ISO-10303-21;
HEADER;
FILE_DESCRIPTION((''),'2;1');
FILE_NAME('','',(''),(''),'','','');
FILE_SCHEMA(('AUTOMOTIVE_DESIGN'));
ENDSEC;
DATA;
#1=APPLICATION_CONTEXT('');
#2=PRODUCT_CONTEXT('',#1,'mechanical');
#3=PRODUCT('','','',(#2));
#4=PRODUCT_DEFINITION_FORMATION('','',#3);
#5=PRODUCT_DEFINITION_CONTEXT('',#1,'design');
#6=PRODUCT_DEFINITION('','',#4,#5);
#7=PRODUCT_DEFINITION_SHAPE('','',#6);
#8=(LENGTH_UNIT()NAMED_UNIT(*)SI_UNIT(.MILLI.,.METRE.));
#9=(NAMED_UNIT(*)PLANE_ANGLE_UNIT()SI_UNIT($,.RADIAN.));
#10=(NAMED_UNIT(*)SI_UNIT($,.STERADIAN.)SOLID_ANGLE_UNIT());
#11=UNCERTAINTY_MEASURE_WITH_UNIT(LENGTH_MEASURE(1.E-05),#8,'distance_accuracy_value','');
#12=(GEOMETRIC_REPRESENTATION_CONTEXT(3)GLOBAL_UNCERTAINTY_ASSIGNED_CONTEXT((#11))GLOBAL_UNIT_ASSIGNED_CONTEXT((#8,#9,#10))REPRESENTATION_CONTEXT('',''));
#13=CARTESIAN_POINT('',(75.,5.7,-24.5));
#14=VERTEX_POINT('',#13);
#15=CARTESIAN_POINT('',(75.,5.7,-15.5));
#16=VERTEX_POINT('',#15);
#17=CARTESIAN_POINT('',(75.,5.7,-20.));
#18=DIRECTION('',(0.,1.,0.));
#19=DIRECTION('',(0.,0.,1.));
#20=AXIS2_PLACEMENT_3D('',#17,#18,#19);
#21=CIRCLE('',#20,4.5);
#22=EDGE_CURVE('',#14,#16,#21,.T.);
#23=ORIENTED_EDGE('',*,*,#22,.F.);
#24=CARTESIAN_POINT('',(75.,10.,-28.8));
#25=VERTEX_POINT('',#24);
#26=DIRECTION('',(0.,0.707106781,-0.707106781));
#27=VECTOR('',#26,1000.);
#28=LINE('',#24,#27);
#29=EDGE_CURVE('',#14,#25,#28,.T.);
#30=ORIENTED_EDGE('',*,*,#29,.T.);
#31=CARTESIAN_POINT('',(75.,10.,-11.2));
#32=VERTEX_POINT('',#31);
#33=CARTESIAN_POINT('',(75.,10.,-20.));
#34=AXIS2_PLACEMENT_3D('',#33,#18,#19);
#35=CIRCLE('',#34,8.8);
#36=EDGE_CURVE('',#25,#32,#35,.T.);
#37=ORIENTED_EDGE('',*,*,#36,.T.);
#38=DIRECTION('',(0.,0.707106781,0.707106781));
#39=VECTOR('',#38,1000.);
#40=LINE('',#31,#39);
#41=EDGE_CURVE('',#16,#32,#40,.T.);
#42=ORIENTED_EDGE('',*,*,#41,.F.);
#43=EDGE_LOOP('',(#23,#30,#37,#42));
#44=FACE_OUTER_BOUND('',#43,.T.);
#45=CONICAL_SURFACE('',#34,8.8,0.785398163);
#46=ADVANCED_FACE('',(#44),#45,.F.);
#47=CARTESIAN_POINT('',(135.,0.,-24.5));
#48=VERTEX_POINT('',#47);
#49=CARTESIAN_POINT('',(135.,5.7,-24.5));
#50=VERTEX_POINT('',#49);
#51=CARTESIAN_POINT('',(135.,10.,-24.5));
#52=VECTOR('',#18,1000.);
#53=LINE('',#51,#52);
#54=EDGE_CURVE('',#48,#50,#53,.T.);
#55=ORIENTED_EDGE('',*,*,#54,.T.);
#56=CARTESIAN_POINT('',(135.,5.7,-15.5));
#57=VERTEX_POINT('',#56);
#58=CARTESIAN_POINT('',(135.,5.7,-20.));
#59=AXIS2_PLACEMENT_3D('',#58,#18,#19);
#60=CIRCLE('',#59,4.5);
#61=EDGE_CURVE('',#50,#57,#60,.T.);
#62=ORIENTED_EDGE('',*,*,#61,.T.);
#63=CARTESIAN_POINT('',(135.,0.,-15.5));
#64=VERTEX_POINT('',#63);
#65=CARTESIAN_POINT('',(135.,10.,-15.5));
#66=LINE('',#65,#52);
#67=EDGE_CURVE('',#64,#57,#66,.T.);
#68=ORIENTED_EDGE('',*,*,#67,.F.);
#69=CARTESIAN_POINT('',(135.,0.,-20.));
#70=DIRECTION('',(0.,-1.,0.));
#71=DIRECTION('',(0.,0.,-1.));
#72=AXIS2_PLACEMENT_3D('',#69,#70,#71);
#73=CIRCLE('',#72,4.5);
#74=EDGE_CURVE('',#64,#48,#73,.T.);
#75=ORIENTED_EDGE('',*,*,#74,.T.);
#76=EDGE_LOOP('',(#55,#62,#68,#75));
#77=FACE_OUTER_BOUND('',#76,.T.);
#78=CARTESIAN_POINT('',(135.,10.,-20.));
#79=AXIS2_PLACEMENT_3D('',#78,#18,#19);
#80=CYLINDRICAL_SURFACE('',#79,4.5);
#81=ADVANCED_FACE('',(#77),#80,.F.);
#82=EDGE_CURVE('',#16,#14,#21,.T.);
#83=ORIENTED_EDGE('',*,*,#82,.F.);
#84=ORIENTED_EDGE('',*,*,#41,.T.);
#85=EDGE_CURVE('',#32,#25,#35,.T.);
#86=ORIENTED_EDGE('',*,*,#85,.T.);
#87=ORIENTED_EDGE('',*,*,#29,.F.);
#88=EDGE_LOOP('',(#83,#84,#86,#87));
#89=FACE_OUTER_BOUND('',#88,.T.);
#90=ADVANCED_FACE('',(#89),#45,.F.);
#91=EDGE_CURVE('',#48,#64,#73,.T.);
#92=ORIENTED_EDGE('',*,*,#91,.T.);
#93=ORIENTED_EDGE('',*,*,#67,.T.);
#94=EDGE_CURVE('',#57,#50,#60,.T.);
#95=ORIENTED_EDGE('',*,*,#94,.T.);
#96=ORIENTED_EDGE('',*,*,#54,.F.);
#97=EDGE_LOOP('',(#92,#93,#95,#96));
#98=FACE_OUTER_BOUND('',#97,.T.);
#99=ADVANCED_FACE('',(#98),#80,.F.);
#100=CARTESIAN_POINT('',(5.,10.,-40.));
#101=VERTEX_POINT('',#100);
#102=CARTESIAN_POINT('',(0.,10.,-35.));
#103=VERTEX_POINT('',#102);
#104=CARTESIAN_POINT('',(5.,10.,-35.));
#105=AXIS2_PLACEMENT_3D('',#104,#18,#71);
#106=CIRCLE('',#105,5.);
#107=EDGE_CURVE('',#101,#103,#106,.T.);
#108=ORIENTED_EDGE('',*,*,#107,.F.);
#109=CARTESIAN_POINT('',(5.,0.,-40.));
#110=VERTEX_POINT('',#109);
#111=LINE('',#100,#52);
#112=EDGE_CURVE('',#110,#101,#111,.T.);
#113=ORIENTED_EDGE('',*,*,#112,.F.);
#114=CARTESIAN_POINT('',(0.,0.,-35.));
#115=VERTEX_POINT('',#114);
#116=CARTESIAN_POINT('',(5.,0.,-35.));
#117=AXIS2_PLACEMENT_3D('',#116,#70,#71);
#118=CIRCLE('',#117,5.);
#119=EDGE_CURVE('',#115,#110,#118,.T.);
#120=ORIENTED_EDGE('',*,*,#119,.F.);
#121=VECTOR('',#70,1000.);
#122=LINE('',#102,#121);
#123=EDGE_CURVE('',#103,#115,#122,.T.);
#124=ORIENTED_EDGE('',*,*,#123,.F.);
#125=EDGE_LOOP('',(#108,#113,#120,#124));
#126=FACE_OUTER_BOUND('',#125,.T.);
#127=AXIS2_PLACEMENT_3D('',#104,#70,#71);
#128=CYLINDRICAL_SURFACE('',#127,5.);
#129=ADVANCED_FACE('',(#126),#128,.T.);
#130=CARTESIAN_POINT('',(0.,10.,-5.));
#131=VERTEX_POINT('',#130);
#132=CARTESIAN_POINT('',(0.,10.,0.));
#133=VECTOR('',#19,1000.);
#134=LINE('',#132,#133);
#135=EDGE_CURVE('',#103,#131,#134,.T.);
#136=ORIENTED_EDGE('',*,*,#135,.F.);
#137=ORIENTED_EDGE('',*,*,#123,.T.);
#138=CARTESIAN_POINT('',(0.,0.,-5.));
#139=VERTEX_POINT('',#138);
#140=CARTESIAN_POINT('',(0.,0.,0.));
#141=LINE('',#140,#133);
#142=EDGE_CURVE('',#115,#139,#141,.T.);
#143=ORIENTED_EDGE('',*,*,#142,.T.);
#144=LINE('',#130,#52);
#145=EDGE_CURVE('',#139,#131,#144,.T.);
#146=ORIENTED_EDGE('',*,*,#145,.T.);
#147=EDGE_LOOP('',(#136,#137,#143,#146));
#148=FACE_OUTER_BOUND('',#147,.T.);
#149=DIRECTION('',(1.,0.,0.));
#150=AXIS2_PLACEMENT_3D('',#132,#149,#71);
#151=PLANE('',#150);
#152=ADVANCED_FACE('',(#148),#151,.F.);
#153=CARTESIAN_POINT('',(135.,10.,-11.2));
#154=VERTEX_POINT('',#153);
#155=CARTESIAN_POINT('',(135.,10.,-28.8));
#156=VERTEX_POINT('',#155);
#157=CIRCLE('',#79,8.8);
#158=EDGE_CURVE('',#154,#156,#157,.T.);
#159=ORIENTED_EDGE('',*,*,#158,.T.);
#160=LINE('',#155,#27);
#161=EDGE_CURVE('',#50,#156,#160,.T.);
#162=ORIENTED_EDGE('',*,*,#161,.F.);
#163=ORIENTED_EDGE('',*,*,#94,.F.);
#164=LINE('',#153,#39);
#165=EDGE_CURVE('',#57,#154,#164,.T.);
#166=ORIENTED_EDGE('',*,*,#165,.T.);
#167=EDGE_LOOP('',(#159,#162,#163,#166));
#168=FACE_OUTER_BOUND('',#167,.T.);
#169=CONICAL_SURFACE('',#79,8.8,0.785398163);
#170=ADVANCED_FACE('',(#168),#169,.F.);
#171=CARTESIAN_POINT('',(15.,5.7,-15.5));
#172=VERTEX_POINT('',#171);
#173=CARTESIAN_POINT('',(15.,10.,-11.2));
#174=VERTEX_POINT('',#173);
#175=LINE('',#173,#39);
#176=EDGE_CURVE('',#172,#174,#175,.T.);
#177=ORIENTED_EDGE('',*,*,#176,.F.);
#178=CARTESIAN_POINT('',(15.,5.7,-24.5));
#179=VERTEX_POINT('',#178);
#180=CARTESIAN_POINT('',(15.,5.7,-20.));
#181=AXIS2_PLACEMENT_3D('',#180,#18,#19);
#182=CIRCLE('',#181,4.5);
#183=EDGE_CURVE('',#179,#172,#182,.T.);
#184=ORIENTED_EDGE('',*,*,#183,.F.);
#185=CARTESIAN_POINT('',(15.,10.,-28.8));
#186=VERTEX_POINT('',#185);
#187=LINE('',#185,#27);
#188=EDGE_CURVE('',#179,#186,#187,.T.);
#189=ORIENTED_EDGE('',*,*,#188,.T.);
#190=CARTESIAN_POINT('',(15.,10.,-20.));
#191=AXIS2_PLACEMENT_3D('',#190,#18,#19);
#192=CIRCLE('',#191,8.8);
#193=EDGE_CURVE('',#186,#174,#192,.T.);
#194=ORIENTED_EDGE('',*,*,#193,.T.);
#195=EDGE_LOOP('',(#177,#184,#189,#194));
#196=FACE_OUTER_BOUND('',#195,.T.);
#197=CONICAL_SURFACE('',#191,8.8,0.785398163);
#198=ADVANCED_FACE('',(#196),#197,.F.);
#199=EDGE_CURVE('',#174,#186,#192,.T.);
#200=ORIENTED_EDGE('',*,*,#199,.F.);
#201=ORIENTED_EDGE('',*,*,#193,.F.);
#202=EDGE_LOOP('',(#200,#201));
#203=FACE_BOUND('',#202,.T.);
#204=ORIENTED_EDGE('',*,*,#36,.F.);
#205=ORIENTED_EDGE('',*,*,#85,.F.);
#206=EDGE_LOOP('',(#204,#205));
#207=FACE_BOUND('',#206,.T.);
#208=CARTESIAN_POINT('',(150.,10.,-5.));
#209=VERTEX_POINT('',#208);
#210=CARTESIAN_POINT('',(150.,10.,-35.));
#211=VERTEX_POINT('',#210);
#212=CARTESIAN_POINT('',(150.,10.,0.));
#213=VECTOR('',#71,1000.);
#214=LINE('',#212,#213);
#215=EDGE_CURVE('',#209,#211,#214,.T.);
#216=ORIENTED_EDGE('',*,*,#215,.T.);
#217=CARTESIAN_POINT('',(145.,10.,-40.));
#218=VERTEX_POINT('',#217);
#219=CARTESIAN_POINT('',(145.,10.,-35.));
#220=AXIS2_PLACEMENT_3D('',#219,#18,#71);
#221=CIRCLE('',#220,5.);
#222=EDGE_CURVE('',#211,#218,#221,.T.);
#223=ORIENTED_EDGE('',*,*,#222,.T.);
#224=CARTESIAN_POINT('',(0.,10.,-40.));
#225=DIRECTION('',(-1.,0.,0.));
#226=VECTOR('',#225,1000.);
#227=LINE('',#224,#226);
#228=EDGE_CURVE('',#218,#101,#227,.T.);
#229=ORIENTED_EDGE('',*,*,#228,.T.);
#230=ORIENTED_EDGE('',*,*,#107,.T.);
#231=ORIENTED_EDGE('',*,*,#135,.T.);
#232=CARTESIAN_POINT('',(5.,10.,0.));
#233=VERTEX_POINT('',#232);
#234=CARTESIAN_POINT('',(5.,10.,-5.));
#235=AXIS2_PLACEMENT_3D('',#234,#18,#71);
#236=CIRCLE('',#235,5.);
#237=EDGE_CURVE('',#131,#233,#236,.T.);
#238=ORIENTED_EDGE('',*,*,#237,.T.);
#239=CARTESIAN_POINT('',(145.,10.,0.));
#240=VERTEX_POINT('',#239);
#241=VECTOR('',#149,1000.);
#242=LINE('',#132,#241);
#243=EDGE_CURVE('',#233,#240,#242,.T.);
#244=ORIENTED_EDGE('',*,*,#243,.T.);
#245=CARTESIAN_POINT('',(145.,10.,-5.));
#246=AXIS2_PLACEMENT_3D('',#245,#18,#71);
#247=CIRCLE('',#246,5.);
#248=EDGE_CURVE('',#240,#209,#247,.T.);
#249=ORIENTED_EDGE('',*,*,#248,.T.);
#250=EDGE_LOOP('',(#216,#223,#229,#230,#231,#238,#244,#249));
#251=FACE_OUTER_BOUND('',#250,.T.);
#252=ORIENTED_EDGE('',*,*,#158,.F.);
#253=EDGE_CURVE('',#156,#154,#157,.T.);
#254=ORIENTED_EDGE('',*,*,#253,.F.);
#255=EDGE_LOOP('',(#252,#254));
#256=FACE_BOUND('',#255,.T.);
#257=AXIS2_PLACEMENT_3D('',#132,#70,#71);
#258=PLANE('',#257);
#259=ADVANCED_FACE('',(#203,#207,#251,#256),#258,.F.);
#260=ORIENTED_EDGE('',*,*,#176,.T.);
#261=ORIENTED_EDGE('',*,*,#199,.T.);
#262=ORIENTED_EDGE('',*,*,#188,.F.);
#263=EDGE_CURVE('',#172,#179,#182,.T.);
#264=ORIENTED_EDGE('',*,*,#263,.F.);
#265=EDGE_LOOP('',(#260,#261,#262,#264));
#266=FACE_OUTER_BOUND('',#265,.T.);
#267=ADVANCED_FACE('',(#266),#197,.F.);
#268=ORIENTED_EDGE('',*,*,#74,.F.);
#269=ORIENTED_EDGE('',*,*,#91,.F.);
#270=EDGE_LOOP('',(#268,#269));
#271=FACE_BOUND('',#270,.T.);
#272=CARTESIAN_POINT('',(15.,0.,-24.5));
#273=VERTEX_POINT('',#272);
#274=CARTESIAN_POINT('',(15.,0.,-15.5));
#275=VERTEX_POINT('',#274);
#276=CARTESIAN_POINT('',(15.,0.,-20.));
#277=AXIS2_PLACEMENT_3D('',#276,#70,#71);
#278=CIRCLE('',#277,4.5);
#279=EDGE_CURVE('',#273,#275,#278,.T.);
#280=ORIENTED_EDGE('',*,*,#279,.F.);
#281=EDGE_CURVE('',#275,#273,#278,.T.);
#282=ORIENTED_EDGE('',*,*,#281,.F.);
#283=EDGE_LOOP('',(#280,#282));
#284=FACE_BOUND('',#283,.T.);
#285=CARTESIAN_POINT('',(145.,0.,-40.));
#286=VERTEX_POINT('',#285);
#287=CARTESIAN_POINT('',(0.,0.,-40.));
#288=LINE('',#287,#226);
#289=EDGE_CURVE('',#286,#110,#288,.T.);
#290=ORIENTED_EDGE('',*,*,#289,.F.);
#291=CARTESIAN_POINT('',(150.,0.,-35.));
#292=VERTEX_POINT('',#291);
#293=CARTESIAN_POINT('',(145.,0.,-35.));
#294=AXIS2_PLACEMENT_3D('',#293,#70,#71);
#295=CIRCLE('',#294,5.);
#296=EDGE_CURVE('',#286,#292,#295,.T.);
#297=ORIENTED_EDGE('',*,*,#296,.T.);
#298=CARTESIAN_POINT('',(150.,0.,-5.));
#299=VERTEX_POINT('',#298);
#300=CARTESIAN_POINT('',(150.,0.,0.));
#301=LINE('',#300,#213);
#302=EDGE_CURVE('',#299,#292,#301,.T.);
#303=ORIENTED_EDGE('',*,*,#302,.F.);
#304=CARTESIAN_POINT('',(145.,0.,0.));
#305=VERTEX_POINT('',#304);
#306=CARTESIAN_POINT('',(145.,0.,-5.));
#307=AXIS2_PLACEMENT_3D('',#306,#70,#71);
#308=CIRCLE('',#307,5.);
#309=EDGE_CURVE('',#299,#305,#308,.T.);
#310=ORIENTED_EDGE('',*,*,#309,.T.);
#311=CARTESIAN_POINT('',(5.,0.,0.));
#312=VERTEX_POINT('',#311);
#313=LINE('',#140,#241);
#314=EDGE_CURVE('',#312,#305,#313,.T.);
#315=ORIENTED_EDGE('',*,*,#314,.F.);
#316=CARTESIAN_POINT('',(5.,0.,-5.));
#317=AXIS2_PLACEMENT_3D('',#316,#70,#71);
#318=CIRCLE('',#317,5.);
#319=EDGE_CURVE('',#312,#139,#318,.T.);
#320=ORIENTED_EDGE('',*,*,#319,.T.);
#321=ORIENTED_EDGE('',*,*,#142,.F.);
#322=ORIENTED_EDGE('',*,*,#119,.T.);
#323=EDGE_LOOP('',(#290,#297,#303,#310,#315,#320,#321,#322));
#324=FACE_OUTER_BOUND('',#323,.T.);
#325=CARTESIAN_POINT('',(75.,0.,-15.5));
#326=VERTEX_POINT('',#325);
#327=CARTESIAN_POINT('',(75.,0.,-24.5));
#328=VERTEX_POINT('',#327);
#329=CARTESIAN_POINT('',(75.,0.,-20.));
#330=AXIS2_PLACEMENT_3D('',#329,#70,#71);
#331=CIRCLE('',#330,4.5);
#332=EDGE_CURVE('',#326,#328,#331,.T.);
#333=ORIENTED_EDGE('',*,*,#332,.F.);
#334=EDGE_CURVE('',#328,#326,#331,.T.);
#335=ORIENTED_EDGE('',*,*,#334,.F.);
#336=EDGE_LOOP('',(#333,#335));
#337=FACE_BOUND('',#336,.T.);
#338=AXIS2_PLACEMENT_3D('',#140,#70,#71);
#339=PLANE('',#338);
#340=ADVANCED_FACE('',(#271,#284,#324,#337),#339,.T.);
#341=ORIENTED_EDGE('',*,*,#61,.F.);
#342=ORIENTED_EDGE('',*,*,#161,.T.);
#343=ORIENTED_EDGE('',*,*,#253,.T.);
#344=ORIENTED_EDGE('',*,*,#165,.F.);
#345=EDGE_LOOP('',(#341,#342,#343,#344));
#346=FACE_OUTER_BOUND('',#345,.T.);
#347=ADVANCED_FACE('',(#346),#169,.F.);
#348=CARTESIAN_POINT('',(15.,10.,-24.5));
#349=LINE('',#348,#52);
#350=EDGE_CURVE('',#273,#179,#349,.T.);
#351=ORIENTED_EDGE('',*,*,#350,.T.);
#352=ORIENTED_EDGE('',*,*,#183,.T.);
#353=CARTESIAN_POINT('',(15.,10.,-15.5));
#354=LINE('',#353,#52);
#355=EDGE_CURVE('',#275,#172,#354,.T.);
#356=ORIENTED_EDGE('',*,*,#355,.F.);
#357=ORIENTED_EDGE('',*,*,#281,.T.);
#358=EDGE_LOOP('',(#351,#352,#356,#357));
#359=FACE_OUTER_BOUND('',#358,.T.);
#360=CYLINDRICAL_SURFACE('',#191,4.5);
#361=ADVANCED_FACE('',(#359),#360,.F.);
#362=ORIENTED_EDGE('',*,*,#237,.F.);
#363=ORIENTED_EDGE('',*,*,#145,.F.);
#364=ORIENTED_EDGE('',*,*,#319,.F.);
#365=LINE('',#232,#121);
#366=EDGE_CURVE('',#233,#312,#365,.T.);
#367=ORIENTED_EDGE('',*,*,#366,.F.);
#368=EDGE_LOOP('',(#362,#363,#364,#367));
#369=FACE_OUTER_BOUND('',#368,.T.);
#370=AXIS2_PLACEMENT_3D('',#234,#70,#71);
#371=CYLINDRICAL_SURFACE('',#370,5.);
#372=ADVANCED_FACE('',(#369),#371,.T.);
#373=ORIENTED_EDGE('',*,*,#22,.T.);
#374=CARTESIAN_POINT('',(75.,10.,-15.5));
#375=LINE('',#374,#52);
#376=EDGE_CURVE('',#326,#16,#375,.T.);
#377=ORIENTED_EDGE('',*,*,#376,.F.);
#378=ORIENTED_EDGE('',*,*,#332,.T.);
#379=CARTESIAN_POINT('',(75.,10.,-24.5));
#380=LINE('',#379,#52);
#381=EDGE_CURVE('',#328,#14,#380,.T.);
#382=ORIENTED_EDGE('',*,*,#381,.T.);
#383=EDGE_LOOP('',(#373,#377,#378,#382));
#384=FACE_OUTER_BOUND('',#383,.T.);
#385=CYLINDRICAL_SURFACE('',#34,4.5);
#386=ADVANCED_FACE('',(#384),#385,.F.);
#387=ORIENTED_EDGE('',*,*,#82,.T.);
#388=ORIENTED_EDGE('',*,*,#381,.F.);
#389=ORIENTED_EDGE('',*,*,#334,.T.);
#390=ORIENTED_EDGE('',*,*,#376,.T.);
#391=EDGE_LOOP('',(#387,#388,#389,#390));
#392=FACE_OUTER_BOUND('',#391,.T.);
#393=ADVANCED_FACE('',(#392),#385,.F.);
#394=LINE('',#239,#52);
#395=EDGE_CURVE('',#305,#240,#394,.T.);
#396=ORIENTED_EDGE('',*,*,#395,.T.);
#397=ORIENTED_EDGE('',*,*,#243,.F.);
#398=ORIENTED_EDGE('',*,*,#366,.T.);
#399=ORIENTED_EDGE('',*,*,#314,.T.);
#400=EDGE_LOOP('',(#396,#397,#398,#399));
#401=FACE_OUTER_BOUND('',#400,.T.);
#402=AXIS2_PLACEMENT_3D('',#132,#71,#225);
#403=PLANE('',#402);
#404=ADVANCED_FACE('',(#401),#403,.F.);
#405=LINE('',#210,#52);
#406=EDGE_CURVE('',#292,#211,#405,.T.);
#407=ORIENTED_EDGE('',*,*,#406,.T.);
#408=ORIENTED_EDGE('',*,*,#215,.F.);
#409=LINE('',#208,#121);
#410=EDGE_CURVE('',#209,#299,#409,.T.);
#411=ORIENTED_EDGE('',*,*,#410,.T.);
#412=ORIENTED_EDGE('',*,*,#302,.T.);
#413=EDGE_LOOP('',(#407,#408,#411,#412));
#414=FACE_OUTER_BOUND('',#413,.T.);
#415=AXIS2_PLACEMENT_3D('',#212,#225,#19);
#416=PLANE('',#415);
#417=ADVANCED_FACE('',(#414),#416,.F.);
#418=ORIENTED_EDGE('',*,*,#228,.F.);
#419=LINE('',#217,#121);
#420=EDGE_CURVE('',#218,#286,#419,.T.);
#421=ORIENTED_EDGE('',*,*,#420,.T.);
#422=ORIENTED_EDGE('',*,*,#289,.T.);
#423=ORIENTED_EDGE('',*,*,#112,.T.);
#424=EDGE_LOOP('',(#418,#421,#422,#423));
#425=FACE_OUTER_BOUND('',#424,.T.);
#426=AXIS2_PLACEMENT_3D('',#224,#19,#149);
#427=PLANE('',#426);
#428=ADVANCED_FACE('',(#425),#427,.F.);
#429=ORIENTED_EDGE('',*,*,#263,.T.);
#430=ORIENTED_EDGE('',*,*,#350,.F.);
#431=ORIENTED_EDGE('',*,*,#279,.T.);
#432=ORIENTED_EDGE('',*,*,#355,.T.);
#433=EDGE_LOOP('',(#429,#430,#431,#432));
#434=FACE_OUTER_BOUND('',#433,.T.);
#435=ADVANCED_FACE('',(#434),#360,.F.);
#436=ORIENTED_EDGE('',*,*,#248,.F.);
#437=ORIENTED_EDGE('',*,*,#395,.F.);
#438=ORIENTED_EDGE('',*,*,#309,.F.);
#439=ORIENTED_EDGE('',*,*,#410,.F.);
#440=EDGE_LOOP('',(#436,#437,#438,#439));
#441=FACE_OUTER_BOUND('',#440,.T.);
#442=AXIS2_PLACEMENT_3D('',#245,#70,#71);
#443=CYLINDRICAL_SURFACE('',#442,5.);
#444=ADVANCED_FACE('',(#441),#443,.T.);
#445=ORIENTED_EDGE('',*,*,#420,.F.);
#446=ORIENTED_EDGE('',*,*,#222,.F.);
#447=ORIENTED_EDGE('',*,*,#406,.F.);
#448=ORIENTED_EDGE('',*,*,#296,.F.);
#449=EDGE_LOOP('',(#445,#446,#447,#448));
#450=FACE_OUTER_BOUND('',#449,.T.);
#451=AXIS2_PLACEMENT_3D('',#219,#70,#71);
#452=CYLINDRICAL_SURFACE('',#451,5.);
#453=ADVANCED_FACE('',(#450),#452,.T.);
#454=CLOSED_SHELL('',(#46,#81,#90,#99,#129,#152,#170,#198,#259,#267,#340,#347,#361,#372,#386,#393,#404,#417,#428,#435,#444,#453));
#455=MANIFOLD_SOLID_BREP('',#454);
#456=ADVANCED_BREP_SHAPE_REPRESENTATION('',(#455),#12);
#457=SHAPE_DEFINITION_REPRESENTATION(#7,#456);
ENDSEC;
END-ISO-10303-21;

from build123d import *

# Parameters (mm, degrees)
SKETCH1_W                                  = 150
SKETCH1_H                                  = 40
BOSS_EXTRUDE1_DEPTH                        = 10
FILLET1_R                                  = 5
SOCKET_BUTTON_HEAD_SCREW_HOLE1_D           = 9
SOCKET_BUTTON_HEAD_SCREW_HOLE1_DEPTH       = 19.75
SOCKET_BUTTON_HEAD_SCREW_HOLE1_CSINK_D     = 17.6
SOCKET_BUTTON_HEAD_SCREW_HOLE1_CSINK_ANGLE = 90
SOCKET_BUTTON_HEAD_SCREW_HOLE1_TIP         = 2.703872786


with BuildPart() as part:
    # Sketch1 → Boss-Extrude1 (new body)
    with BuildSketch(Plane(origin=(0, 0, 0), x_dir=(1, 0, 0), z_dir=(0, 1, 0))):
        with Locations((75, 20)):
            Rectangle(SKETCH1_W, SKETCH1_H)
    extrude(amount=BOSS_EXTRUDE1_DEPTH)

    # Fillet1
    fillet1_edges = [part.edges().sort_by_distance(p)[0] for p in [
        (0, 5, -40),
        (150, 5, -40),
        (150, 5, 0),
        (0, 5, 0),
    ]]
    fillet(fillet1_edges, radius=FILLET1_R)

    # Socket Button Head Screw Hole1
    with Locations(Plane(origin=(0, 10, 0), x_dir=(1, 0, 0), z_dir=(0, 1, 0))):
        with Locations((75, 20), (15, 20), (135, 20)):
            CounterSinkHole(SOCKET_BUTTON_HEAD_SCREW_HOLE1_D / 2, SOCKET_BUTTON_HEAD_SCREW_HOLE1_CSINK_D / 2, depth=SOCKET_BUTTON_HEAD_SCREW_HOLE1_DEPTH, counter_sink_angle=SOCKET_BUTTON_HEAD_SCREW_HOLE1_CSINK_ANGLE)
            with Locations((0, 0, -(SOCKET_BUTTON_HEAD_SCREW_HOLE1_DEPTH + SOCKET_BUTTON_HEAD_SCREW_HOLE1_TIP / 2))):  # 118° drill point
                Cone(0, SOCKET_BUTTON_HEAD_SCREW_HOLE1_D / 2, SOCKET_BUTTON_HEAD_SCREW_HOLE1_TIP, mode=Mode.SUBTRACT)


solid = part.part
